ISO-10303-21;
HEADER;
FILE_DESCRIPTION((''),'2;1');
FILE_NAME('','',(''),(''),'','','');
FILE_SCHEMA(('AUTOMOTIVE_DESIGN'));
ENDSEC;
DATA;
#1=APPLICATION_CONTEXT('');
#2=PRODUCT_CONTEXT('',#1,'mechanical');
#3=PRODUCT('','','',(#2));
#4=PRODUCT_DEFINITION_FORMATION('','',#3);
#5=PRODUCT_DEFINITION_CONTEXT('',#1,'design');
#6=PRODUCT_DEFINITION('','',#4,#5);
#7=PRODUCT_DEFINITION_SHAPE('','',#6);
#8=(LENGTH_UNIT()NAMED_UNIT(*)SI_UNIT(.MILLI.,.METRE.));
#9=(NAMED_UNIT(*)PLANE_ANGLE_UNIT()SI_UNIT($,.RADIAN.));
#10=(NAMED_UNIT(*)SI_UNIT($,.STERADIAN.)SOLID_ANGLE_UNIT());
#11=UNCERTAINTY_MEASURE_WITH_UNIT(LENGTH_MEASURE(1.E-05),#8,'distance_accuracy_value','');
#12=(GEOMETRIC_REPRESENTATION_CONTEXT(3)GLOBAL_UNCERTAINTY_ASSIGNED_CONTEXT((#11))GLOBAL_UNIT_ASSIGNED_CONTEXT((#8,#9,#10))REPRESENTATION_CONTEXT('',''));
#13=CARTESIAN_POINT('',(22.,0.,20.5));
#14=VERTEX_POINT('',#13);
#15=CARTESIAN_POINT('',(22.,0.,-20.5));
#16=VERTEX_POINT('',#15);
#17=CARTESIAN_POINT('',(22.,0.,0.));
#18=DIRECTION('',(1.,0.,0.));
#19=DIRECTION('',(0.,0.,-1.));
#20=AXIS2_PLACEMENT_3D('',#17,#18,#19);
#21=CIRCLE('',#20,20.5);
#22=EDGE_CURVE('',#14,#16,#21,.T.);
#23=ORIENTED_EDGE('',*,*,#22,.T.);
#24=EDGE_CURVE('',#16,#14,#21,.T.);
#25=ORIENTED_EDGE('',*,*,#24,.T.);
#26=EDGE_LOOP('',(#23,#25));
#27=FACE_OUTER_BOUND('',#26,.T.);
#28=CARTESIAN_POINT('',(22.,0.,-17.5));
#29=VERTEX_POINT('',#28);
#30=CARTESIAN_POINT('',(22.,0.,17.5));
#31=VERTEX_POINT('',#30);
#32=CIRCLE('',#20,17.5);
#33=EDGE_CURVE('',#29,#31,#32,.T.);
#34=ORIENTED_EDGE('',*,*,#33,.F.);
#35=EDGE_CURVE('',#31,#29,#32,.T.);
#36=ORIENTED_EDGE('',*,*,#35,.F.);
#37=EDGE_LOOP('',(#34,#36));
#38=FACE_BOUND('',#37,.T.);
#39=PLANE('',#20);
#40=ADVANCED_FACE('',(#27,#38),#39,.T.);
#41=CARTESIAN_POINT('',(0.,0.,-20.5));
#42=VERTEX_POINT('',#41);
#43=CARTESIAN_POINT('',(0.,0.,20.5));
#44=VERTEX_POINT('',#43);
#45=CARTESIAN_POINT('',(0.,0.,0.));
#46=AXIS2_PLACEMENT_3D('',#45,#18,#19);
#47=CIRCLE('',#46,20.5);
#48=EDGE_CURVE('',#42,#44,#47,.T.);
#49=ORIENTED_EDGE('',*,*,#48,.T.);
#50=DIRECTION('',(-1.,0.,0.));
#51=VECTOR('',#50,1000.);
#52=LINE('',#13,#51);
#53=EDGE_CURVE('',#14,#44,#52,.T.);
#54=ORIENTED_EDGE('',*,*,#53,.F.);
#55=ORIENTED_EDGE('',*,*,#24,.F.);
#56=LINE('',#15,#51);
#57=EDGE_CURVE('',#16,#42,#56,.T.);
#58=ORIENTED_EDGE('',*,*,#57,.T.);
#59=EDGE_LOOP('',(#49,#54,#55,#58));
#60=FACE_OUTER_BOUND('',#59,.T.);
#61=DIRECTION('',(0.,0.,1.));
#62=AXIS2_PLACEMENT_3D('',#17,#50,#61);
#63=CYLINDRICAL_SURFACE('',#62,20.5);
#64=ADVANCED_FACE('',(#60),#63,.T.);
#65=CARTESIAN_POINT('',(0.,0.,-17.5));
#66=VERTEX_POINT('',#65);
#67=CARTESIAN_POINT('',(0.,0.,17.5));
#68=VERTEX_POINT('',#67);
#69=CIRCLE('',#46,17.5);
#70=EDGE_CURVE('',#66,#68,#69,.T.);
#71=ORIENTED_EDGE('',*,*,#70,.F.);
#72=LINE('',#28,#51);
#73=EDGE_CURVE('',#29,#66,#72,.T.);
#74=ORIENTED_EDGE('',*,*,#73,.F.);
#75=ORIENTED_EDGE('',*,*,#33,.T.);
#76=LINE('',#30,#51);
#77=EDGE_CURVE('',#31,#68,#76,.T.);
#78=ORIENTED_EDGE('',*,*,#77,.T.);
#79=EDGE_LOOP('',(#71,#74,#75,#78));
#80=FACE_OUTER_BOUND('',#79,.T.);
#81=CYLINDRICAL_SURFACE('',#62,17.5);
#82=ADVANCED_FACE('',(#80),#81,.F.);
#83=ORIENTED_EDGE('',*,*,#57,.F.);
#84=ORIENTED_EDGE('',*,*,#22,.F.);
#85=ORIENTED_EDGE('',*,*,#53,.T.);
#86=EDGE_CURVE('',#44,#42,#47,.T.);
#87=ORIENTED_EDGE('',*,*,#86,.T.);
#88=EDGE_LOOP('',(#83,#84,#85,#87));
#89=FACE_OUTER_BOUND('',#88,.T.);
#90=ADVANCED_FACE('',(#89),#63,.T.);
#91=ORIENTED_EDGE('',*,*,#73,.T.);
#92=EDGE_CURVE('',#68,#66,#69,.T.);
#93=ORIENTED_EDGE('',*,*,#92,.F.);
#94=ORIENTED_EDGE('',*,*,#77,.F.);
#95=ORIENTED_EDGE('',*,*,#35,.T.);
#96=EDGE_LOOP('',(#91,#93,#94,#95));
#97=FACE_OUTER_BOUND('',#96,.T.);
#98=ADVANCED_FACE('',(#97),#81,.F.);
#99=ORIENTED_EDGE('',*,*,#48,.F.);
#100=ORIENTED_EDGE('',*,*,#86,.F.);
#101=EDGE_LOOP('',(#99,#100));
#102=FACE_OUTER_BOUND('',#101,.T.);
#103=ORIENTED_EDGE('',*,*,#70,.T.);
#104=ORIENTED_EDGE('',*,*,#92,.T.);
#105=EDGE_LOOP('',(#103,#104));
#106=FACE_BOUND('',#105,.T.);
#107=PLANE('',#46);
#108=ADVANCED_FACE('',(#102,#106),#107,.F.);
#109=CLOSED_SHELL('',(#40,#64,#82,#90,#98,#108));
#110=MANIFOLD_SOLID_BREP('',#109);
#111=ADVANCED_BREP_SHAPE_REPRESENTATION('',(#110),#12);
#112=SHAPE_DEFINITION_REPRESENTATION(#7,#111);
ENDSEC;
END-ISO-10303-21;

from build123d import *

# Parameters (mm, degrees)
SKETCH_1_R      = 20.5
SKETCH_1_R_2    = 17.5
EXTRUDE_1_DEPTH = 22


with BuildPart() as part:
    # 草图1 → 凸台-拉伸1 (new body)
    with BuildSketch(Plane(origin=(0, 0, 0), x_dir=(0, 0, -1), z_dir=(1, 0, 0))):
        Circle(SKETCH_1_R)
        Circle(SKETCH_1_R_2, mode=Mode.SUBTRACT)
    extrude(amount=EXTRUDE_1_DEPTH)


solid = part.part
